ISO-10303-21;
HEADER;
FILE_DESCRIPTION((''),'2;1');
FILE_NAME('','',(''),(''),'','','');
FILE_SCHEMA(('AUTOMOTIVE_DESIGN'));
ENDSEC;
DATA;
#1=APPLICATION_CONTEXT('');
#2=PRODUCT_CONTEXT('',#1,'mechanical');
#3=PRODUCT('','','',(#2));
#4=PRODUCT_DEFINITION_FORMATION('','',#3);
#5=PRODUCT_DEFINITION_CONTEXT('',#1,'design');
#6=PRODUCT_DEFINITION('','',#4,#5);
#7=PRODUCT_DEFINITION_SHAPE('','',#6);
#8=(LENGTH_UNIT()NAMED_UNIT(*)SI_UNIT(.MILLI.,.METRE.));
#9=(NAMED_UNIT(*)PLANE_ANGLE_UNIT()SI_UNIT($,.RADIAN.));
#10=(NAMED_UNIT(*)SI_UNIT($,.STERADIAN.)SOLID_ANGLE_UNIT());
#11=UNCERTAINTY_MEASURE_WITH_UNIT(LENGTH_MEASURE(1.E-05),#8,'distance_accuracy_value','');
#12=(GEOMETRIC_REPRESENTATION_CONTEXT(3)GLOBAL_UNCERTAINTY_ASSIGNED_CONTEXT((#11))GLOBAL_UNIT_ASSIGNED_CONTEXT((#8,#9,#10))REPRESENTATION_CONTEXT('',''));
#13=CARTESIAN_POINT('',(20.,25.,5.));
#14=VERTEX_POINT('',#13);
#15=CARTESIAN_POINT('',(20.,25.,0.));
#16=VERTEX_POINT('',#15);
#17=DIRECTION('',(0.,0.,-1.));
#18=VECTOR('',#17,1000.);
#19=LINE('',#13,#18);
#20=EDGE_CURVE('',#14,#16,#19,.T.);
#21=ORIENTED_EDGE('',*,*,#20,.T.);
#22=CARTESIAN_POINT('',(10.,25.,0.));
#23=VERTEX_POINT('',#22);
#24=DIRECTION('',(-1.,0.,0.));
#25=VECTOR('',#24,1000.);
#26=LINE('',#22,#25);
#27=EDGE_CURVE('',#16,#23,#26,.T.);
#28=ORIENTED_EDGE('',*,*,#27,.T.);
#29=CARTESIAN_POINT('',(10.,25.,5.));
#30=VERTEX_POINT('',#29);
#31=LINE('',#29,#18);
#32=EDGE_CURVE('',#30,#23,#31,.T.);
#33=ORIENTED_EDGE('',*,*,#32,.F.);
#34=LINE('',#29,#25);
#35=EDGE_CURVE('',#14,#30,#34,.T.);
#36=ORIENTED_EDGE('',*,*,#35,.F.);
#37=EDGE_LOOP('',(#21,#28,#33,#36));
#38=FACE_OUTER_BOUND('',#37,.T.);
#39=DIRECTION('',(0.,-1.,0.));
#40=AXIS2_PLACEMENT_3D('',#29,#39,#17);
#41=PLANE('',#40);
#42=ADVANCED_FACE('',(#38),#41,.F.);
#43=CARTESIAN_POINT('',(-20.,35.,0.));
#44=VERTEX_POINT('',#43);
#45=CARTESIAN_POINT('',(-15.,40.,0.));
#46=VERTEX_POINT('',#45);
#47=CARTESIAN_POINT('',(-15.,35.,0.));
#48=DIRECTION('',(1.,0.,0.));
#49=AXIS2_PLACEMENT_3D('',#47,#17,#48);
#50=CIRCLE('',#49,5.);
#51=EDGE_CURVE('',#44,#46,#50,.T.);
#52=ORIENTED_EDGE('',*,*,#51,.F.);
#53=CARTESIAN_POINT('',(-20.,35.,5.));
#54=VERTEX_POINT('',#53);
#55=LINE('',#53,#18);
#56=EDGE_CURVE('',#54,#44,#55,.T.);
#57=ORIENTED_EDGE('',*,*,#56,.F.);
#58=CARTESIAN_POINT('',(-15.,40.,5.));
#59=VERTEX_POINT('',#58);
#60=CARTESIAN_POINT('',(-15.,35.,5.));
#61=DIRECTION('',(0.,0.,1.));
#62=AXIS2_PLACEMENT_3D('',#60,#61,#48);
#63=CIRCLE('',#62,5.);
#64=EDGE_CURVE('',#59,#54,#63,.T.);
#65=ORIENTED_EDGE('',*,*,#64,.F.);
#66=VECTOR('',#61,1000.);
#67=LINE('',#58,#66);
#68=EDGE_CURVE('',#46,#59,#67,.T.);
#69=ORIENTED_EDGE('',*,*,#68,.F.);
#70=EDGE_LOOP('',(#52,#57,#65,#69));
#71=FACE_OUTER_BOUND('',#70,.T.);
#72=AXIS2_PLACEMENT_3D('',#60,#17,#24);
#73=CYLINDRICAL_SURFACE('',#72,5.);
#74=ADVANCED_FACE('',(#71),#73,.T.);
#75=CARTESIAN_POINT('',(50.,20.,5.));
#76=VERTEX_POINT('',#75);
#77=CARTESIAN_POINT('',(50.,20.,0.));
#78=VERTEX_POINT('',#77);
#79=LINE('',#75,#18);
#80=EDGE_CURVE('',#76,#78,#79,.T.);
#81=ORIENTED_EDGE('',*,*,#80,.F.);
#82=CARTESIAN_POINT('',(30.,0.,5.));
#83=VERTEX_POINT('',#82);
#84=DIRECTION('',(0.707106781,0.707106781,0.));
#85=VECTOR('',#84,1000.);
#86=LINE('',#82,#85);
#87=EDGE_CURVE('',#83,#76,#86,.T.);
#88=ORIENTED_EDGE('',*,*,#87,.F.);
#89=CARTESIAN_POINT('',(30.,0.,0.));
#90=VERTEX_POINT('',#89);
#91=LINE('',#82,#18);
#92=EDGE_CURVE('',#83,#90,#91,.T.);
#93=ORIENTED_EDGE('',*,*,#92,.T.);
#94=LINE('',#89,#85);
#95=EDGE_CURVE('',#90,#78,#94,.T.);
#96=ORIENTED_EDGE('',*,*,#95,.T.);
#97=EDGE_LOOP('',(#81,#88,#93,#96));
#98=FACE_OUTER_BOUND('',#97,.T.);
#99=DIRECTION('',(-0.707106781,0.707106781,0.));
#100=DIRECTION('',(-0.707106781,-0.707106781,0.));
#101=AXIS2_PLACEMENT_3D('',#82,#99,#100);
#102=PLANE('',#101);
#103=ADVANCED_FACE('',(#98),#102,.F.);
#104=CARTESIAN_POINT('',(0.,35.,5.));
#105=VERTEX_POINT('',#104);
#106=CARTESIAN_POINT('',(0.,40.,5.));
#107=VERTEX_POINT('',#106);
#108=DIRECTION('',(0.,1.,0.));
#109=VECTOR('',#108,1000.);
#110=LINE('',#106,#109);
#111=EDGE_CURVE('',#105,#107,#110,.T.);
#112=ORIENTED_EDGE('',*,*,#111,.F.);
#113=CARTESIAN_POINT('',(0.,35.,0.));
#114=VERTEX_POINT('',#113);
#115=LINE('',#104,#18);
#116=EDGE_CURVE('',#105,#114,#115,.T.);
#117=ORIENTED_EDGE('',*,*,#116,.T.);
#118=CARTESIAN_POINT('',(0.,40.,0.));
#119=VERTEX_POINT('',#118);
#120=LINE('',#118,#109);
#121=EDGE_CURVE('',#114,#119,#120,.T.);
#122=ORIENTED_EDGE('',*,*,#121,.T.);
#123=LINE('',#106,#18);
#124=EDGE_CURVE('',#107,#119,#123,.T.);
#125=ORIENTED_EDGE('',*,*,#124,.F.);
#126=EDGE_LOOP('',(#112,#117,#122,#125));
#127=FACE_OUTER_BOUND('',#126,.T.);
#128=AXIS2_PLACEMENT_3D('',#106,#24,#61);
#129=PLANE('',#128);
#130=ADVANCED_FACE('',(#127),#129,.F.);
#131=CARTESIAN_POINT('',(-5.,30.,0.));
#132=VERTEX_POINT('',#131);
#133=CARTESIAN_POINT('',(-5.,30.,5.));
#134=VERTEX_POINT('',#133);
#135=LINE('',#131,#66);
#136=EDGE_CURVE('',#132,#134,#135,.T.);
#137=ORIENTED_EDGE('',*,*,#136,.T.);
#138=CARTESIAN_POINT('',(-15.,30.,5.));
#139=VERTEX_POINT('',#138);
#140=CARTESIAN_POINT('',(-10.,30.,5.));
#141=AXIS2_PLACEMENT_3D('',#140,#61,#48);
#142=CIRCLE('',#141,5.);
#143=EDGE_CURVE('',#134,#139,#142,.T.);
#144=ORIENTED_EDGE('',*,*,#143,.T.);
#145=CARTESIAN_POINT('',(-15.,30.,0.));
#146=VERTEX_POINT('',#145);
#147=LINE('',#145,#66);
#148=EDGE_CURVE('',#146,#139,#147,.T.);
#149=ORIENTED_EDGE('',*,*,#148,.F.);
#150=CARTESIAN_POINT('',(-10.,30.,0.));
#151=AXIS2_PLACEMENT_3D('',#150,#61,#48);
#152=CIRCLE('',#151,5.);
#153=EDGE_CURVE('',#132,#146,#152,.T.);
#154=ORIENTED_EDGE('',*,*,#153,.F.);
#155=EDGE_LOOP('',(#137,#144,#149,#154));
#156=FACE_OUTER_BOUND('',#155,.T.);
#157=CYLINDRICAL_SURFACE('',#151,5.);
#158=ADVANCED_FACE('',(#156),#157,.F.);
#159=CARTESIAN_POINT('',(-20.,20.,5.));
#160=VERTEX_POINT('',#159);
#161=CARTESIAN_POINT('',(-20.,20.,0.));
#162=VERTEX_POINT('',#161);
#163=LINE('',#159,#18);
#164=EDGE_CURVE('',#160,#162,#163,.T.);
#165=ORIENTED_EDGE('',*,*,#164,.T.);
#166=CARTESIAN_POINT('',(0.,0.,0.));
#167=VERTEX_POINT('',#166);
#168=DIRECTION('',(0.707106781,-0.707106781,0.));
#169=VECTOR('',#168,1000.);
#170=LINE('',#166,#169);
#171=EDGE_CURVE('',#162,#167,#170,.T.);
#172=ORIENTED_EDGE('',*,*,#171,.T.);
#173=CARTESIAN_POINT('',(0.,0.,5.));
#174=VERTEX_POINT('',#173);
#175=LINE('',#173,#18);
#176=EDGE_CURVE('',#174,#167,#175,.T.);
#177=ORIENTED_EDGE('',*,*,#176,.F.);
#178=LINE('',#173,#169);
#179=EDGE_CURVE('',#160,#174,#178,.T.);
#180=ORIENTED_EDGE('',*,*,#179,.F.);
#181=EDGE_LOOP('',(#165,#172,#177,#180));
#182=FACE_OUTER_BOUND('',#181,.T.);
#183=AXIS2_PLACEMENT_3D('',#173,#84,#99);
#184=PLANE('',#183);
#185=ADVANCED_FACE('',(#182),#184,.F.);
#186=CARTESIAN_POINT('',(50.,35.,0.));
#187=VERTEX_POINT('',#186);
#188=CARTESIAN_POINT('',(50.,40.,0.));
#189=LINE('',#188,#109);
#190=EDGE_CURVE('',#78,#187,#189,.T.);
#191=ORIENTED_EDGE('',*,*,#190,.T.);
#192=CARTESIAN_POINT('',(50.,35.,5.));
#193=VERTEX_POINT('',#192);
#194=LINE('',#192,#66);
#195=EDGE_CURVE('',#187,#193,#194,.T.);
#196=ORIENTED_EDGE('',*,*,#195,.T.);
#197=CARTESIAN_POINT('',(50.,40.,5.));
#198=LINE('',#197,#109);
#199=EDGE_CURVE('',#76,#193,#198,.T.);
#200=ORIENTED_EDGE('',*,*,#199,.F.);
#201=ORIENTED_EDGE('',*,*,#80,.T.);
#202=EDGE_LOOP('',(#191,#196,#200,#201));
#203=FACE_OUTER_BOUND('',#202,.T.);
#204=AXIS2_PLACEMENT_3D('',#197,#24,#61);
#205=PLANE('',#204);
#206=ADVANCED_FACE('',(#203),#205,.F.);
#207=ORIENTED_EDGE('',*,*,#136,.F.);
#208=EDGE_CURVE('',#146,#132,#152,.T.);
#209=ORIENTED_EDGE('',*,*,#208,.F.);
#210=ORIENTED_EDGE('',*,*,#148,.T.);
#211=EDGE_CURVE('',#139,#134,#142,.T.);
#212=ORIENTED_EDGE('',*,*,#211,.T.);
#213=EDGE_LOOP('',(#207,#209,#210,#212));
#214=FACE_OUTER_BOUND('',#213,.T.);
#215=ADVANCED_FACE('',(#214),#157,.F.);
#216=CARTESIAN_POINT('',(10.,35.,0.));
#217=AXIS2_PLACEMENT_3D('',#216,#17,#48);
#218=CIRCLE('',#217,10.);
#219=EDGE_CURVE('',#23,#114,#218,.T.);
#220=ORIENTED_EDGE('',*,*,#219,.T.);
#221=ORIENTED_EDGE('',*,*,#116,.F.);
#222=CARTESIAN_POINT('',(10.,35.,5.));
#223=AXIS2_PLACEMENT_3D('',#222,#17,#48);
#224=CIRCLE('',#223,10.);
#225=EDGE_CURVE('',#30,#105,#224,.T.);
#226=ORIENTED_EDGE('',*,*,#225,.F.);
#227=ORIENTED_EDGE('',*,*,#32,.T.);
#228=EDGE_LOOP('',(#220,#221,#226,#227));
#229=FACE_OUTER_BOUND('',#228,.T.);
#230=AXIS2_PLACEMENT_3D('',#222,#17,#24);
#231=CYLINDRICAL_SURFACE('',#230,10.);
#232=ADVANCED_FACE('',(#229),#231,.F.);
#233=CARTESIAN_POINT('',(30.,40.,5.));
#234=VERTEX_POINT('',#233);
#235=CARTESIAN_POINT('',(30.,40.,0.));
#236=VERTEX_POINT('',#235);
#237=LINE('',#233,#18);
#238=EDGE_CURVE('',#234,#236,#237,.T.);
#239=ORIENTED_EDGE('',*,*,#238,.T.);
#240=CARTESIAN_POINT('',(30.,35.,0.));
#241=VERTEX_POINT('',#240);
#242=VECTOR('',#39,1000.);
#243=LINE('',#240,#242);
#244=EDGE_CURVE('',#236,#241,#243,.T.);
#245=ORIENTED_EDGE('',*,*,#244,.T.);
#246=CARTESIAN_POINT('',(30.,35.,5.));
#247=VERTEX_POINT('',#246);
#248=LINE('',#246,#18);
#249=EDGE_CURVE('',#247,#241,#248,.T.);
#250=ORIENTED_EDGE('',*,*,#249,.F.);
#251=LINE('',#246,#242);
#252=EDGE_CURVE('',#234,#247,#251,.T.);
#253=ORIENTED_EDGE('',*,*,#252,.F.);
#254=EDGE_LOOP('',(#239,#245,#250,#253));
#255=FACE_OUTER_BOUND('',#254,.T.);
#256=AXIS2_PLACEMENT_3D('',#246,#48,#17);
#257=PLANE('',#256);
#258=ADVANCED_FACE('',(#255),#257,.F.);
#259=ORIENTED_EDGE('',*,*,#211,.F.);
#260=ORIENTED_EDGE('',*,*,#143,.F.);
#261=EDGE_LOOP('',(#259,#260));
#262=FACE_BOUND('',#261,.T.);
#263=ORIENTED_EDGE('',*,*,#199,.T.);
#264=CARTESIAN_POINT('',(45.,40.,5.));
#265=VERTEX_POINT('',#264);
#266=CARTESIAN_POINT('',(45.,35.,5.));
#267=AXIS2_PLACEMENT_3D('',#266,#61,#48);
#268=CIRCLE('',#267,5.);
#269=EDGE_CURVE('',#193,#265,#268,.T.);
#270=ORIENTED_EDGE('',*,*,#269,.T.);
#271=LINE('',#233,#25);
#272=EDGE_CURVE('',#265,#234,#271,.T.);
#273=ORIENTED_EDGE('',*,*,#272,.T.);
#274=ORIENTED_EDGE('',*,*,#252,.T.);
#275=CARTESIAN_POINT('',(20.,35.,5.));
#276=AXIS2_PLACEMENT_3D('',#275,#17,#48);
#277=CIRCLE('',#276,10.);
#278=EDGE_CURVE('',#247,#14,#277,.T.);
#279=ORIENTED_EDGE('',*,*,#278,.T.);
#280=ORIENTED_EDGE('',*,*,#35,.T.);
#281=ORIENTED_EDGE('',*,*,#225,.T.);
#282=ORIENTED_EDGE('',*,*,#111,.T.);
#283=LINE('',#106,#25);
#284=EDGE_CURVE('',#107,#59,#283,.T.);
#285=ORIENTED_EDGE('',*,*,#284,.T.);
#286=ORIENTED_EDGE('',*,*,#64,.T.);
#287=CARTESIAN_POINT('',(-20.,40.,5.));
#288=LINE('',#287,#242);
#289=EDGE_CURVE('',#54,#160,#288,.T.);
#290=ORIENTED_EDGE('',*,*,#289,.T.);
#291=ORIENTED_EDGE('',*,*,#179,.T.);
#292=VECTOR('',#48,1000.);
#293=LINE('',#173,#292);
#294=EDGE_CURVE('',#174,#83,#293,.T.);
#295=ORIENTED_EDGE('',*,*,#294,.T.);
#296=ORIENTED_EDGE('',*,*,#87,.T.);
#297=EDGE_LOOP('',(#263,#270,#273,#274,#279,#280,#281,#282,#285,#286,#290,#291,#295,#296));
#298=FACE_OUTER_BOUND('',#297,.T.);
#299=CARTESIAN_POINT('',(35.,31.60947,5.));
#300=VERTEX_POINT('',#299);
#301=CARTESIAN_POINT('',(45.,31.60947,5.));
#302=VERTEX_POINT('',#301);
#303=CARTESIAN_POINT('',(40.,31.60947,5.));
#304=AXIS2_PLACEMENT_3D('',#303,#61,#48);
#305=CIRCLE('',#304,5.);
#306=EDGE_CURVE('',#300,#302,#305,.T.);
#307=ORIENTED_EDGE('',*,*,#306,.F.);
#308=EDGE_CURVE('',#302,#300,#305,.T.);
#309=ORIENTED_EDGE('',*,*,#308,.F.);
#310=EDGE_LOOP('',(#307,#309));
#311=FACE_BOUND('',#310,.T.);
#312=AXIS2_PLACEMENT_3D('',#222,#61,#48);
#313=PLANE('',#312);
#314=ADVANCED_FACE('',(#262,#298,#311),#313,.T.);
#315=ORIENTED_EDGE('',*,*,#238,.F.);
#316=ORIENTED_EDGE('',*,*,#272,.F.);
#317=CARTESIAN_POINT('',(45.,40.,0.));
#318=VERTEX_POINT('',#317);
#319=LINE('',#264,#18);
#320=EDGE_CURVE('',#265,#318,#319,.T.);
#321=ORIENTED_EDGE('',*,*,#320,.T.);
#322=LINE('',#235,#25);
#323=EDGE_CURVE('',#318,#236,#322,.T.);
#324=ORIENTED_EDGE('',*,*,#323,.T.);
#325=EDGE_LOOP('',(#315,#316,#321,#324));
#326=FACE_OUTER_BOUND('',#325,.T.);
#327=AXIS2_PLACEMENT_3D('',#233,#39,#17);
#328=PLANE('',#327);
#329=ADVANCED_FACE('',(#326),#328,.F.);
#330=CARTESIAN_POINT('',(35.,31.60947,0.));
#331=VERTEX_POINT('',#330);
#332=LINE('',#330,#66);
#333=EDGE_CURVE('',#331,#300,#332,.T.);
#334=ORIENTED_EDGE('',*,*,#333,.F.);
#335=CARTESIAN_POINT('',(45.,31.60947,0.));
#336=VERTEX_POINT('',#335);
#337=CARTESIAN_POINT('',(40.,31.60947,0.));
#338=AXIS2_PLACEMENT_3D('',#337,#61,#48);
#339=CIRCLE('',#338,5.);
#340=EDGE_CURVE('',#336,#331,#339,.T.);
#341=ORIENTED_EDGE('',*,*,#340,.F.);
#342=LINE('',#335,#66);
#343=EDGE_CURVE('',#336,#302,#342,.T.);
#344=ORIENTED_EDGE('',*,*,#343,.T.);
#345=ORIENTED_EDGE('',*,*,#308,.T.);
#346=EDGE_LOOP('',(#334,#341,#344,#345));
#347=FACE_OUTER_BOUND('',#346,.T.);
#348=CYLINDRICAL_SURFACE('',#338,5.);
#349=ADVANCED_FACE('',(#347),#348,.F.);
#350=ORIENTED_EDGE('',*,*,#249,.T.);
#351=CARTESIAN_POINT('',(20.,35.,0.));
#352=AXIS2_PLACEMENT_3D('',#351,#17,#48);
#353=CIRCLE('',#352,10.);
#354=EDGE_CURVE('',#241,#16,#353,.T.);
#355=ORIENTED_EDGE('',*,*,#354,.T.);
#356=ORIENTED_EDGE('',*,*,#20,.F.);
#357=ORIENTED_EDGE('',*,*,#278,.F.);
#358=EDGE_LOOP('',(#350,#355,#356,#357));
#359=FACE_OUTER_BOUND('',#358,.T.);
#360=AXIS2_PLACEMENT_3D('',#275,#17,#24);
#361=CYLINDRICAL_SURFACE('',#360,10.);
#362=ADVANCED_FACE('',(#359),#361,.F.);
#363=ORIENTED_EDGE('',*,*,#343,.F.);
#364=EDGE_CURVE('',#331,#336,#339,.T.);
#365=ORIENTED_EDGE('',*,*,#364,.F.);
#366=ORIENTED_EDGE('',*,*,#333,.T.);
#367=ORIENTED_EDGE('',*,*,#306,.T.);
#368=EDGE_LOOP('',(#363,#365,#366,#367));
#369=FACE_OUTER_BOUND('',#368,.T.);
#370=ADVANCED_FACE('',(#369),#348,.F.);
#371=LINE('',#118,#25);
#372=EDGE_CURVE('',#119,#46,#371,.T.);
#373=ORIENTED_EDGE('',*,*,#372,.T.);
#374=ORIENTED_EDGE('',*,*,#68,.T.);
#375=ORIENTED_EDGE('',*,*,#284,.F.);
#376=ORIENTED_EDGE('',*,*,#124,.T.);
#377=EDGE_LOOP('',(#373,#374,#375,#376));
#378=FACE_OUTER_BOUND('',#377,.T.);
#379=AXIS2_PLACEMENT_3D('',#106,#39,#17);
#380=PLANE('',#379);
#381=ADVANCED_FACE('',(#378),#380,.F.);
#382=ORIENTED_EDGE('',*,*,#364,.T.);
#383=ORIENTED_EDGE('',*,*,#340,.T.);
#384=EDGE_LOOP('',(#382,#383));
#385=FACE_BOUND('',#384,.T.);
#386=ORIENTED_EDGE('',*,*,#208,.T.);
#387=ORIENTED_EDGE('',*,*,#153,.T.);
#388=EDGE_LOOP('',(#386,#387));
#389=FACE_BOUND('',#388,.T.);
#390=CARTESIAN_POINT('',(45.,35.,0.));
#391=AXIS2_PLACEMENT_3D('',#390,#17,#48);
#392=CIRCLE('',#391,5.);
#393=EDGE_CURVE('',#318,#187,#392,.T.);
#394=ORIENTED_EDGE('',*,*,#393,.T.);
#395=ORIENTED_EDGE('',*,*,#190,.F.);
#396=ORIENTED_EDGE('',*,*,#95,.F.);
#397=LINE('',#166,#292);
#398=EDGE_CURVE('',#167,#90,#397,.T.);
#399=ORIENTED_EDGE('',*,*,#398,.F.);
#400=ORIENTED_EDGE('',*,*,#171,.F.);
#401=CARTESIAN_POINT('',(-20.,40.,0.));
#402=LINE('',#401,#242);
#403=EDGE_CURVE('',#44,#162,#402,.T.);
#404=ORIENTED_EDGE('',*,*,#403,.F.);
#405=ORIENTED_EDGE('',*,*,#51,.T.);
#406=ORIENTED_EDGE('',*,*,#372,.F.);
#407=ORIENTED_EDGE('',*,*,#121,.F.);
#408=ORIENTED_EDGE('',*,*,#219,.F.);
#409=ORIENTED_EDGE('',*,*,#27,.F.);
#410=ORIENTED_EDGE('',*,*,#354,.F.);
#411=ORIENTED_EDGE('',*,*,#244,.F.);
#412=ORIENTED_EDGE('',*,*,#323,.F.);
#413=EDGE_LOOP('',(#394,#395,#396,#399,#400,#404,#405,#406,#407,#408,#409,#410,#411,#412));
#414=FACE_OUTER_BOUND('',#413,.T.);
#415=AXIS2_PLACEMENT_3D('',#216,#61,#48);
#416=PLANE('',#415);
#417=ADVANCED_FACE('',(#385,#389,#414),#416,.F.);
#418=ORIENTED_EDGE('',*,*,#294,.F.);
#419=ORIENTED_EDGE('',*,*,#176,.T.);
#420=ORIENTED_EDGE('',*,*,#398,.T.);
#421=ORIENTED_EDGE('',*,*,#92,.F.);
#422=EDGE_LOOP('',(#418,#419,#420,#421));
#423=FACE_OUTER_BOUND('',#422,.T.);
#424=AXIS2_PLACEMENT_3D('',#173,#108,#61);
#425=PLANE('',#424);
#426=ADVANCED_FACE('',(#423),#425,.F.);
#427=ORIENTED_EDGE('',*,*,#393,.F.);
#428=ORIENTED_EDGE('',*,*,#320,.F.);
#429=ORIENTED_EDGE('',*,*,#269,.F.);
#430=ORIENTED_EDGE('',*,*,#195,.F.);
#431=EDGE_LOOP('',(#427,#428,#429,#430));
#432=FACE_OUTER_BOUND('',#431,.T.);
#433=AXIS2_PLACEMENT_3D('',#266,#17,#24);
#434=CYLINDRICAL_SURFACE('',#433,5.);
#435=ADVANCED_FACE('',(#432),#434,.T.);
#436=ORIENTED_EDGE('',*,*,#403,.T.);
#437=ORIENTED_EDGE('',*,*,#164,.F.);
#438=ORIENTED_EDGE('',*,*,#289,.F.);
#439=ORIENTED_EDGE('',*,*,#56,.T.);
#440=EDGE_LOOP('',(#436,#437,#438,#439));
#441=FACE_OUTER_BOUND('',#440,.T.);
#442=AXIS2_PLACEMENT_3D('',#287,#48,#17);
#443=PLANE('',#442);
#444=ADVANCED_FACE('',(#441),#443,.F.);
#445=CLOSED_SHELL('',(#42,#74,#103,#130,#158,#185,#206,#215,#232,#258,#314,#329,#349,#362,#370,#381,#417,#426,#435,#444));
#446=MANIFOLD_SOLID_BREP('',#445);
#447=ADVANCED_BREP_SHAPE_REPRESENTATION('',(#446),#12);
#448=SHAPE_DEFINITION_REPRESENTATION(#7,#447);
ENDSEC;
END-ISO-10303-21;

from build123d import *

# Parameters (mm, degrees)
BRACKET_PLATE_DEPTH      = 5
MOUNTING_HOLE_A_SKETCH_R = 5
MOUNTING_HOLE_A_10_DEPTH = 5
MOUNTING_HOLE_B_SKETCH_R = 5
MOUNTING_HOLE_B_10_DEPTH = 5
CORNER_FILLETS_R5_R      = 5


with BuildPart() as part:
    # Bracket Profile Sketch → Bracket Plate (new body)
    with BuildSketch(Plane.XY):
        with BuildLine():
            Line((0, 0), (30, 0))
            Line((30, 0), (50, 20))
            Line((50, 20), (50, 40))
            Line((50, 40), (30, 40))
            Line((30, 40), (30, 35))
            ThreePointArc((30, 35), (27.071067812, 27.928932188), (20, 25))
            Line((20, 25), (10, 25))
            ThreePointArc((10, 25), (2.928932188, 27.928932188), (0, 35))
            Line((0, 35), (0, 40))
            Line((0, 40), (-20, 40))
            Line((-20, 40), (-20, 20))
            Line((-20, 20), (0, 0))
        make_face()
    extrude(amount=BRACKET_PLATE_DEPTH)

    # Mounting Hole A Sketch → Mounting Hole A Ø10 (cut)
    with BuildSketch(Plane.XY.offset(5)):
        with Locations((-10, 30)):
            Circle(MOUNTING_HOLE_A_SKETCH_R)
    extrude(amount=-MOUNTING_HOLE_A_10_DEPTH, mode=Mode.SUBTRACT)

    # Mounting Hole B Sketch → Mounting Hole B Ø10 (cut)
    with BuildSketch(Plane.XY.offset(5)):
        with Locations((40, 31.609469521)):
            Circle(MOUNTING_HOLE_B_SKETCH_R)
    extrude(amount=-MOUNTING_HOLE_B_10_DEPTH, mode=Mode.SUBTRACT)

    # Corner Fillets R5
    corner_fillets_r5_edges = [part.edges().sort_by_distance(p)[0] for p in [
        (-20, 40, 2.5),
        (50, 40, 2.5),
    ]]
    fillet(corner_fillets_r5_edges, radius=CORNER_FILLETS_R5_R)


solid = part.part
